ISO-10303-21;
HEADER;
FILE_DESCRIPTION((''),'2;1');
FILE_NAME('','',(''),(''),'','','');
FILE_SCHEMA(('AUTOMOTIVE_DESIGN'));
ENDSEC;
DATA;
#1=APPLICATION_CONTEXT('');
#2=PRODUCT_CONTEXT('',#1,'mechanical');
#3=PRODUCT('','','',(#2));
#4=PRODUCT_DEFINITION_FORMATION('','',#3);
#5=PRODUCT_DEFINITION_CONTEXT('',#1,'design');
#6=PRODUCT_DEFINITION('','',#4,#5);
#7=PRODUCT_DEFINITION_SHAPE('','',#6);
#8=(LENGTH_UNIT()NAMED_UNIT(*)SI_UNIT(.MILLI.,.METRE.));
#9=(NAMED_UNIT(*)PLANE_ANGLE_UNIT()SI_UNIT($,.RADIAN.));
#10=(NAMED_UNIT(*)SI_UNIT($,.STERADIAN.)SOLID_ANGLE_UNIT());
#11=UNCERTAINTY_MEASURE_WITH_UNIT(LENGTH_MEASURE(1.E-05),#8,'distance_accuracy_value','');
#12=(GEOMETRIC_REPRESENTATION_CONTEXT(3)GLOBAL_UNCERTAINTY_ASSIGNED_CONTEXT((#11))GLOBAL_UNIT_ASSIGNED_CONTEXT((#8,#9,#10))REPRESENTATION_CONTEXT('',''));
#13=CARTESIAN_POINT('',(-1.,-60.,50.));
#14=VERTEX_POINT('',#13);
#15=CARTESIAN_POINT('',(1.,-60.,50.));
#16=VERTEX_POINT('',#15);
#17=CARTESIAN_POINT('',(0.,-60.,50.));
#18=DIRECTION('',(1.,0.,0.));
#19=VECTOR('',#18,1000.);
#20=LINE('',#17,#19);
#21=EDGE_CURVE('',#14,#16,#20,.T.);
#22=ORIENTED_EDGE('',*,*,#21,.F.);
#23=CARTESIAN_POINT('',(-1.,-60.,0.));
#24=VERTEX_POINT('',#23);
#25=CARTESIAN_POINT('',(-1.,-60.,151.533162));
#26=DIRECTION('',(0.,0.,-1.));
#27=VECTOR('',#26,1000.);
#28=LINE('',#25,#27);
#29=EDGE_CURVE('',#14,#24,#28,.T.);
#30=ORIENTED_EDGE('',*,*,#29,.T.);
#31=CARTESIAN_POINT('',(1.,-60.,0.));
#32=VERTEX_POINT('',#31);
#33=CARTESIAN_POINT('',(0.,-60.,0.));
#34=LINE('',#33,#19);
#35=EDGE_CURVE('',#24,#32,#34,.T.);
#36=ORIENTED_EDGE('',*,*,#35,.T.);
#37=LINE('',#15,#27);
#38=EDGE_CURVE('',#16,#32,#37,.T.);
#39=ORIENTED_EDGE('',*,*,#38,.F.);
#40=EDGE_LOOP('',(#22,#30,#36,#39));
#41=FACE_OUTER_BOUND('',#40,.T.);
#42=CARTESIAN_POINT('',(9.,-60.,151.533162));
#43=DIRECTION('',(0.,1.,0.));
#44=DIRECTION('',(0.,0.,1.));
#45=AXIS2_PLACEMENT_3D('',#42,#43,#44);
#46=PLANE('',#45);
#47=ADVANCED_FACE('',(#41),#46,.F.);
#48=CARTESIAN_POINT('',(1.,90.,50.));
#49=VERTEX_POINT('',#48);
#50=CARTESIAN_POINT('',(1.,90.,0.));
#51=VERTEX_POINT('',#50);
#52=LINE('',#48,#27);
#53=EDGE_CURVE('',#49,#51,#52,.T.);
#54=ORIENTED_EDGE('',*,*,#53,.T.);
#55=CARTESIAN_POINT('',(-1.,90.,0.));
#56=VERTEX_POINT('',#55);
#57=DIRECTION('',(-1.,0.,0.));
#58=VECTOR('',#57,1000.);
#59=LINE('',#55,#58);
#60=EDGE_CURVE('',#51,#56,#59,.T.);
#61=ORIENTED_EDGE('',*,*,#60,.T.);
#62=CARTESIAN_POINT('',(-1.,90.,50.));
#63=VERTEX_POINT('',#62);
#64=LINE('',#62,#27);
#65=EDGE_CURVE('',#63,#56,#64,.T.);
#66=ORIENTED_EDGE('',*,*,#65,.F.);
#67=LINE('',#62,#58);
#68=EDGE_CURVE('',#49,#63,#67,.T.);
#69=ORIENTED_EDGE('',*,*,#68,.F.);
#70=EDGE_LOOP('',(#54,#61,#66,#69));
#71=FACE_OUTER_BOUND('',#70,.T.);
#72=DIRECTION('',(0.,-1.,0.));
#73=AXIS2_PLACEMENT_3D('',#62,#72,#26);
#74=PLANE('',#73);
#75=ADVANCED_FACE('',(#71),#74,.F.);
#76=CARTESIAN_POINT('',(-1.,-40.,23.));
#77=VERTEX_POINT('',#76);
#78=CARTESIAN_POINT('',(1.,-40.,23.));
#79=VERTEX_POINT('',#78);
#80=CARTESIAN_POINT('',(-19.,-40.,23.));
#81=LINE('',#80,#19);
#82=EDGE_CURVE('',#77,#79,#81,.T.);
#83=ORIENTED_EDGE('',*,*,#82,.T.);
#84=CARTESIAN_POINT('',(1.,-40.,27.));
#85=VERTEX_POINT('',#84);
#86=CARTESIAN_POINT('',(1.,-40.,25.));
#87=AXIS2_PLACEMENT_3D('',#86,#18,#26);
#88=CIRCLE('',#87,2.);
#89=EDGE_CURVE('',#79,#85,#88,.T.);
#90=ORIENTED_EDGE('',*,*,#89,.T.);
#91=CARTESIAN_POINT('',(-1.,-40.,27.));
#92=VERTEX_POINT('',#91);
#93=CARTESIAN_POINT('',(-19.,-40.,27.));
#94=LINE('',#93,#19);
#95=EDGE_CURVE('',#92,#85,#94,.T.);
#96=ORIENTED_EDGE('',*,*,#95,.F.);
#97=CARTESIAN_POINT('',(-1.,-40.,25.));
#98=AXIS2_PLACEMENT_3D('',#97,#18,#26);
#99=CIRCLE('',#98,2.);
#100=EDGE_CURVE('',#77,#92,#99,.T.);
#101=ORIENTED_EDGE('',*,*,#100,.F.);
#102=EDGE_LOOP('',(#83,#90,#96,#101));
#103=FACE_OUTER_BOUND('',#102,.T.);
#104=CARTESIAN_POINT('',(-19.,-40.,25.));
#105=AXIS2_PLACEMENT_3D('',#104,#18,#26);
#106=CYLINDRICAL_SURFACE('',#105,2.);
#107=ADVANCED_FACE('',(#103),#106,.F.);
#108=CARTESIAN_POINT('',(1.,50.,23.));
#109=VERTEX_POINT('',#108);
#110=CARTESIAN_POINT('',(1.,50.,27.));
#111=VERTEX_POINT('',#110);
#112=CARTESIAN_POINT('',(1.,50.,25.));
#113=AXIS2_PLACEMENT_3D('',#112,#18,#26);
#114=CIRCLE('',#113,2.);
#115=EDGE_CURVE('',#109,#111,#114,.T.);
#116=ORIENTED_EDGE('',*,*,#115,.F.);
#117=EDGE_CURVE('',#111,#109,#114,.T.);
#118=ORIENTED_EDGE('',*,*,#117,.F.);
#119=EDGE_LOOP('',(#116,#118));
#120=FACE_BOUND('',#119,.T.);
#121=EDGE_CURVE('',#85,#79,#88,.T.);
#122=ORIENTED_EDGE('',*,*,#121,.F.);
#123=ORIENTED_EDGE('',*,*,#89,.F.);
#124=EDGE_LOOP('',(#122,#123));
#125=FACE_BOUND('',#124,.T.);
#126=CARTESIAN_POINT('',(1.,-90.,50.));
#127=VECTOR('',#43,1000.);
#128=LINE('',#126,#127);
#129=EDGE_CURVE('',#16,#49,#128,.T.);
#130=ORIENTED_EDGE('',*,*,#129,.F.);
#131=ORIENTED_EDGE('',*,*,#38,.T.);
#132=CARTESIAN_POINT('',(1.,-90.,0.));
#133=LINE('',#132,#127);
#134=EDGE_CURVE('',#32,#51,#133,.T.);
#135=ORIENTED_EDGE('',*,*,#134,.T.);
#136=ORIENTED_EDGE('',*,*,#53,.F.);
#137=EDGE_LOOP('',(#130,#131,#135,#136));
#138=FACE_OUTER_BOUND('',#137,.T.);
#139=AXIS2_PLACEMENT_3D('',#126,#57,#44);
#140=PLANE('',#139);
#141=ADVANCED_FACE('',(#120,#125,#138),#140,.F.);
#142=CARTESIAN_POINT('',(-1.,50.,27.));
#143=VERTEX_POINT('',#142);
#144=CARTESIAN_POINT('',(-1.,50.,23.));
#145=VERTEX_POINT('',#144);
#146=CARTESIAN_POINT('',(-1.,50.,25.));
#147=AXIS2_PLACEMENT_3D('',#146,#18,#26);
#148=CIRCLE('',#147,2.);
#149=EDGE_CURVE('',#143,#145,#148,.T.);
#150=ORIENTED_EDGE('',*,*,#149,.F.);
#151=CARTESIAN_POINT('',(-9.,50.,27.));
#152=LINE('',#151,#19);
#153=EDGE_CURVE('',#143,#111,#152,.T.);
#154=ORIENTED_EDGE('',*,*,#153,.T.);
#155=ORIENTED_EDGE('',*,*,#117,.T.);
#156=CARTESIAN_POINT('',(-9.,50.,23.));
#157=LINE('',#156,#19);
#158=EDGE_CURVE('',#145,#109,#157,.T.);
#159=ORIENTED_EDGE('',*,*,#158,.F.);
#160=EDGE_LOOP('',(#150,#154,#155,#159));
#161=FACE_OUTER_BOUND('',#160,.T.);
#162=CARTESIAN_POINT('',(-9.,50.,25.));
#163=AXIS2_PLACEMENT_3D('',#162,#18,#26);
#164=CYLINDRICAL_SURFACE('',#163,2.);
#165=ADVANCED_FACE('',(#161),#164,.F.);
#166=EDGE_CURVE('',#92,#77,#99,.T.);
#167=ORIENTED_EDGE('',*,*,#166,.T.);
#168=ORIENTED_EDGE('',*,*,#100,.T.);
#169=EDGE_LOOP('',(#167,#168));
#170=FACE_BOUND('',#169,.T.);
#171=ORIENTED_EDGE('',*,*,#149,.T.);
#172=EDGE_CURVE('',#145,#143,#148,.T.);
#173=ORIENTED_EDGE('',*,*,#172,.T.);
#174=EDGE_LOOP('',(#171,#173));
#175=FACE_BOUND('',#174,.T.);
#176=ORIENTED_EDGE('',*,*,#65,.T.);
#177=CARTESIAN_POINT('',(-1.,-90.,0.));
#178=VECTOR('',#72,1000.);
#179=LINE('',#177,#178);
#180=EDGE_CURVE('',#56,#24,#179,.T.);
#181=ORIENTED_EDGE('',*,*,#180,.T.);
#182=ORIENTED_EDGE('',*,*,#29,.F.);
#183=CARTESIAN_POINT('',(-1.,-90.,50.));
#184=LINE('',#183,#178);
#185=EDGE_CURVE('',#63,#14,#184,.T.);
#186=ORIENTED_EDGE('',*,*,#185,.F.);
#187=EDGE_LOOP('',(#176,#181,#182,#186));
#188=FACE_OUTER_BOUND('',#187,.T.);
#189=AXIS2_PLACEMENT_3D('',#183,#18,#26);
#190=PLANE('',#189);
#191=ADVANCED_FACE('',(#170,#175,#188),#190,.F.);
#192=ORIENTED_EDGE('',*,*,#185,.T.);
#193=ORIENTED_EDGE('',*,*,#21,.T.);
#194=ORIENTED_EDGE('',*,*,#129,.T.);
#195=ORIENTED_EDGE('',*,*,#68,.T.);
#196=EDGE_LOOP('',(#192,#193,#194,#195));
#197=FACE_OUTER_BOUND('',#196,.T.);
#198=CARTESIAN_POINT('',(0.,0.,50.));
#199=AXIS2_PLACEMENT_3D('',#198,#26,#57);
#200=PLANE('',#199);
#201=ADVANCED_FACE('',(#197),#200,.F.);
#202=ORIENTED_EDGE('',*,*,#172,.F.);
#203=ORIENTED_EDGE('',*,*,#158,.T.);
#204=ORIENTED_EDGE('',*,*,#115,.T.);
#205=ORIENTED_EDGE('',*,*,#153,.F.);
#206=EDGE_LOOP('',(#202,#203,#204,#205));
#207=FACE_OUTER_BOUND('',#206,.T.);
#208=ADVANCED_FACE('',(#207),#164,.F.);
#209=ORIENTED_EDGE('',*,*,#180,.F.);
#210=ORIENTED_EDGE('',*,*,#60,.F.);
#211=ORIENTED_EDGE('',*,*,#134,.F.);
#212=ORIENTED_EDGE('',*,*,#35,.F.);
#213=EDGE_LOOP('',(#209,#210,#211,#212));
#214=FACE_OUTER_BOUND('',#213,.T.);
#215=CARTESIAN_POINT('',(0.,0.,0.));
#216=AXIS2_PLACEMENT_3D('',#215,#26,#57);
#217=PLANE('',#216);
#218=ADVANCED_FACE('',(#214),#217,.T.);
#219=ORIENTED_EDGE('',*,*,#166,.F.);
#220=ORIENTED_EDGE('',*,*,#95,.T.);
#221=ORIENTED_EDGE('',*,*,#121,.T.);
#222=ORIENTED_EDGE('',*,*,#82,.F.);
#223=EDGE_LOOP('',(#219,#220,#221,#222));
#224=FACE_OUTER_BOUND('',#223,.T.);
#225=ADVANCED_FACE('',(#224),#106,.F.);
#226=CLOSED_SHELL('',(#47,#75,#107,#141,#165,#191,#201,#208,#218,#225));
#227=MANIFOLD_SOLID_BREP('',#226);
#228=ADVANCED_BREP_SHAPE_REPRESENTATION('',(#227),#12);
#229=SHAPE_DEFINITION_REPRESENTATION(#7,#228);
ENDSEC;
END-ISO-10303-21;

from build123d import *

# Parameters (mm, degrees)
SKETCH_1_W          = 2
SKETCH_1_H          = 180
EXTRUDE_1_DEPTH     = 50
SKETCH_2_R          = 2
CUT_EXTRUDE_1_DEPTH = 20
SKETCH_3_R          = 2
CUT_EXTRUDE_2_DEPTH = 10
SKETCH_4_W          = 190.004489292
SKETCH_4_H          = 85.174426234
CUT_EXTRUDE_3_DEPTH = 10


with BuildPart() as part:
    # 草图1 → 凸台-拉伸1 (new body)
    with BuildSketch(Plane.XY):
        Rectangle(SKETCH_1_W, SKETCH_1_H)
    extrude(amount=EXTRUDE_1_DEPTH)

    # 草图2 → 切除-拉伸1 (cut)
    with BuildSketch(Plane(origin=(1, 0, 0), x_dir=(0, 0, -1), z_dir=(1, 0, 0))):
        with Locations((-25, -40)):
            Circle(SKETCH_2_R)
    extrude(amount=-CUT_EXTRUDE_1_DEPTH, mode=Mode.SUBTRACT)

    # 草图3 → 切除-拉伸2 (cut)
    with BuildSketch(Plane(origin=(1, 0, 0), x_dir=(0, 0, -1), z_dir=(1, 0, 0))):
        with Locations((-25, 50)):
            Circle(SKETCH_3_R)
    extrude(amount=-CUT_EXTRUDE_2_DEPTH, mode=Mode.SUBTRACT)

    # 草图4 → 切除-拉伸3 (cut)
    with BuildSketch(Plane.ZY.offset(1)):
        with Locations((56.530917404, -102.587213117)):
            Rectangle(SKETCH_4_W, SKETCH_4_H)
    extrude(amount=-CUT_EXTRUDE_3_DEPTH, mode=Mode.SUBTRACT)


solid = part.part
